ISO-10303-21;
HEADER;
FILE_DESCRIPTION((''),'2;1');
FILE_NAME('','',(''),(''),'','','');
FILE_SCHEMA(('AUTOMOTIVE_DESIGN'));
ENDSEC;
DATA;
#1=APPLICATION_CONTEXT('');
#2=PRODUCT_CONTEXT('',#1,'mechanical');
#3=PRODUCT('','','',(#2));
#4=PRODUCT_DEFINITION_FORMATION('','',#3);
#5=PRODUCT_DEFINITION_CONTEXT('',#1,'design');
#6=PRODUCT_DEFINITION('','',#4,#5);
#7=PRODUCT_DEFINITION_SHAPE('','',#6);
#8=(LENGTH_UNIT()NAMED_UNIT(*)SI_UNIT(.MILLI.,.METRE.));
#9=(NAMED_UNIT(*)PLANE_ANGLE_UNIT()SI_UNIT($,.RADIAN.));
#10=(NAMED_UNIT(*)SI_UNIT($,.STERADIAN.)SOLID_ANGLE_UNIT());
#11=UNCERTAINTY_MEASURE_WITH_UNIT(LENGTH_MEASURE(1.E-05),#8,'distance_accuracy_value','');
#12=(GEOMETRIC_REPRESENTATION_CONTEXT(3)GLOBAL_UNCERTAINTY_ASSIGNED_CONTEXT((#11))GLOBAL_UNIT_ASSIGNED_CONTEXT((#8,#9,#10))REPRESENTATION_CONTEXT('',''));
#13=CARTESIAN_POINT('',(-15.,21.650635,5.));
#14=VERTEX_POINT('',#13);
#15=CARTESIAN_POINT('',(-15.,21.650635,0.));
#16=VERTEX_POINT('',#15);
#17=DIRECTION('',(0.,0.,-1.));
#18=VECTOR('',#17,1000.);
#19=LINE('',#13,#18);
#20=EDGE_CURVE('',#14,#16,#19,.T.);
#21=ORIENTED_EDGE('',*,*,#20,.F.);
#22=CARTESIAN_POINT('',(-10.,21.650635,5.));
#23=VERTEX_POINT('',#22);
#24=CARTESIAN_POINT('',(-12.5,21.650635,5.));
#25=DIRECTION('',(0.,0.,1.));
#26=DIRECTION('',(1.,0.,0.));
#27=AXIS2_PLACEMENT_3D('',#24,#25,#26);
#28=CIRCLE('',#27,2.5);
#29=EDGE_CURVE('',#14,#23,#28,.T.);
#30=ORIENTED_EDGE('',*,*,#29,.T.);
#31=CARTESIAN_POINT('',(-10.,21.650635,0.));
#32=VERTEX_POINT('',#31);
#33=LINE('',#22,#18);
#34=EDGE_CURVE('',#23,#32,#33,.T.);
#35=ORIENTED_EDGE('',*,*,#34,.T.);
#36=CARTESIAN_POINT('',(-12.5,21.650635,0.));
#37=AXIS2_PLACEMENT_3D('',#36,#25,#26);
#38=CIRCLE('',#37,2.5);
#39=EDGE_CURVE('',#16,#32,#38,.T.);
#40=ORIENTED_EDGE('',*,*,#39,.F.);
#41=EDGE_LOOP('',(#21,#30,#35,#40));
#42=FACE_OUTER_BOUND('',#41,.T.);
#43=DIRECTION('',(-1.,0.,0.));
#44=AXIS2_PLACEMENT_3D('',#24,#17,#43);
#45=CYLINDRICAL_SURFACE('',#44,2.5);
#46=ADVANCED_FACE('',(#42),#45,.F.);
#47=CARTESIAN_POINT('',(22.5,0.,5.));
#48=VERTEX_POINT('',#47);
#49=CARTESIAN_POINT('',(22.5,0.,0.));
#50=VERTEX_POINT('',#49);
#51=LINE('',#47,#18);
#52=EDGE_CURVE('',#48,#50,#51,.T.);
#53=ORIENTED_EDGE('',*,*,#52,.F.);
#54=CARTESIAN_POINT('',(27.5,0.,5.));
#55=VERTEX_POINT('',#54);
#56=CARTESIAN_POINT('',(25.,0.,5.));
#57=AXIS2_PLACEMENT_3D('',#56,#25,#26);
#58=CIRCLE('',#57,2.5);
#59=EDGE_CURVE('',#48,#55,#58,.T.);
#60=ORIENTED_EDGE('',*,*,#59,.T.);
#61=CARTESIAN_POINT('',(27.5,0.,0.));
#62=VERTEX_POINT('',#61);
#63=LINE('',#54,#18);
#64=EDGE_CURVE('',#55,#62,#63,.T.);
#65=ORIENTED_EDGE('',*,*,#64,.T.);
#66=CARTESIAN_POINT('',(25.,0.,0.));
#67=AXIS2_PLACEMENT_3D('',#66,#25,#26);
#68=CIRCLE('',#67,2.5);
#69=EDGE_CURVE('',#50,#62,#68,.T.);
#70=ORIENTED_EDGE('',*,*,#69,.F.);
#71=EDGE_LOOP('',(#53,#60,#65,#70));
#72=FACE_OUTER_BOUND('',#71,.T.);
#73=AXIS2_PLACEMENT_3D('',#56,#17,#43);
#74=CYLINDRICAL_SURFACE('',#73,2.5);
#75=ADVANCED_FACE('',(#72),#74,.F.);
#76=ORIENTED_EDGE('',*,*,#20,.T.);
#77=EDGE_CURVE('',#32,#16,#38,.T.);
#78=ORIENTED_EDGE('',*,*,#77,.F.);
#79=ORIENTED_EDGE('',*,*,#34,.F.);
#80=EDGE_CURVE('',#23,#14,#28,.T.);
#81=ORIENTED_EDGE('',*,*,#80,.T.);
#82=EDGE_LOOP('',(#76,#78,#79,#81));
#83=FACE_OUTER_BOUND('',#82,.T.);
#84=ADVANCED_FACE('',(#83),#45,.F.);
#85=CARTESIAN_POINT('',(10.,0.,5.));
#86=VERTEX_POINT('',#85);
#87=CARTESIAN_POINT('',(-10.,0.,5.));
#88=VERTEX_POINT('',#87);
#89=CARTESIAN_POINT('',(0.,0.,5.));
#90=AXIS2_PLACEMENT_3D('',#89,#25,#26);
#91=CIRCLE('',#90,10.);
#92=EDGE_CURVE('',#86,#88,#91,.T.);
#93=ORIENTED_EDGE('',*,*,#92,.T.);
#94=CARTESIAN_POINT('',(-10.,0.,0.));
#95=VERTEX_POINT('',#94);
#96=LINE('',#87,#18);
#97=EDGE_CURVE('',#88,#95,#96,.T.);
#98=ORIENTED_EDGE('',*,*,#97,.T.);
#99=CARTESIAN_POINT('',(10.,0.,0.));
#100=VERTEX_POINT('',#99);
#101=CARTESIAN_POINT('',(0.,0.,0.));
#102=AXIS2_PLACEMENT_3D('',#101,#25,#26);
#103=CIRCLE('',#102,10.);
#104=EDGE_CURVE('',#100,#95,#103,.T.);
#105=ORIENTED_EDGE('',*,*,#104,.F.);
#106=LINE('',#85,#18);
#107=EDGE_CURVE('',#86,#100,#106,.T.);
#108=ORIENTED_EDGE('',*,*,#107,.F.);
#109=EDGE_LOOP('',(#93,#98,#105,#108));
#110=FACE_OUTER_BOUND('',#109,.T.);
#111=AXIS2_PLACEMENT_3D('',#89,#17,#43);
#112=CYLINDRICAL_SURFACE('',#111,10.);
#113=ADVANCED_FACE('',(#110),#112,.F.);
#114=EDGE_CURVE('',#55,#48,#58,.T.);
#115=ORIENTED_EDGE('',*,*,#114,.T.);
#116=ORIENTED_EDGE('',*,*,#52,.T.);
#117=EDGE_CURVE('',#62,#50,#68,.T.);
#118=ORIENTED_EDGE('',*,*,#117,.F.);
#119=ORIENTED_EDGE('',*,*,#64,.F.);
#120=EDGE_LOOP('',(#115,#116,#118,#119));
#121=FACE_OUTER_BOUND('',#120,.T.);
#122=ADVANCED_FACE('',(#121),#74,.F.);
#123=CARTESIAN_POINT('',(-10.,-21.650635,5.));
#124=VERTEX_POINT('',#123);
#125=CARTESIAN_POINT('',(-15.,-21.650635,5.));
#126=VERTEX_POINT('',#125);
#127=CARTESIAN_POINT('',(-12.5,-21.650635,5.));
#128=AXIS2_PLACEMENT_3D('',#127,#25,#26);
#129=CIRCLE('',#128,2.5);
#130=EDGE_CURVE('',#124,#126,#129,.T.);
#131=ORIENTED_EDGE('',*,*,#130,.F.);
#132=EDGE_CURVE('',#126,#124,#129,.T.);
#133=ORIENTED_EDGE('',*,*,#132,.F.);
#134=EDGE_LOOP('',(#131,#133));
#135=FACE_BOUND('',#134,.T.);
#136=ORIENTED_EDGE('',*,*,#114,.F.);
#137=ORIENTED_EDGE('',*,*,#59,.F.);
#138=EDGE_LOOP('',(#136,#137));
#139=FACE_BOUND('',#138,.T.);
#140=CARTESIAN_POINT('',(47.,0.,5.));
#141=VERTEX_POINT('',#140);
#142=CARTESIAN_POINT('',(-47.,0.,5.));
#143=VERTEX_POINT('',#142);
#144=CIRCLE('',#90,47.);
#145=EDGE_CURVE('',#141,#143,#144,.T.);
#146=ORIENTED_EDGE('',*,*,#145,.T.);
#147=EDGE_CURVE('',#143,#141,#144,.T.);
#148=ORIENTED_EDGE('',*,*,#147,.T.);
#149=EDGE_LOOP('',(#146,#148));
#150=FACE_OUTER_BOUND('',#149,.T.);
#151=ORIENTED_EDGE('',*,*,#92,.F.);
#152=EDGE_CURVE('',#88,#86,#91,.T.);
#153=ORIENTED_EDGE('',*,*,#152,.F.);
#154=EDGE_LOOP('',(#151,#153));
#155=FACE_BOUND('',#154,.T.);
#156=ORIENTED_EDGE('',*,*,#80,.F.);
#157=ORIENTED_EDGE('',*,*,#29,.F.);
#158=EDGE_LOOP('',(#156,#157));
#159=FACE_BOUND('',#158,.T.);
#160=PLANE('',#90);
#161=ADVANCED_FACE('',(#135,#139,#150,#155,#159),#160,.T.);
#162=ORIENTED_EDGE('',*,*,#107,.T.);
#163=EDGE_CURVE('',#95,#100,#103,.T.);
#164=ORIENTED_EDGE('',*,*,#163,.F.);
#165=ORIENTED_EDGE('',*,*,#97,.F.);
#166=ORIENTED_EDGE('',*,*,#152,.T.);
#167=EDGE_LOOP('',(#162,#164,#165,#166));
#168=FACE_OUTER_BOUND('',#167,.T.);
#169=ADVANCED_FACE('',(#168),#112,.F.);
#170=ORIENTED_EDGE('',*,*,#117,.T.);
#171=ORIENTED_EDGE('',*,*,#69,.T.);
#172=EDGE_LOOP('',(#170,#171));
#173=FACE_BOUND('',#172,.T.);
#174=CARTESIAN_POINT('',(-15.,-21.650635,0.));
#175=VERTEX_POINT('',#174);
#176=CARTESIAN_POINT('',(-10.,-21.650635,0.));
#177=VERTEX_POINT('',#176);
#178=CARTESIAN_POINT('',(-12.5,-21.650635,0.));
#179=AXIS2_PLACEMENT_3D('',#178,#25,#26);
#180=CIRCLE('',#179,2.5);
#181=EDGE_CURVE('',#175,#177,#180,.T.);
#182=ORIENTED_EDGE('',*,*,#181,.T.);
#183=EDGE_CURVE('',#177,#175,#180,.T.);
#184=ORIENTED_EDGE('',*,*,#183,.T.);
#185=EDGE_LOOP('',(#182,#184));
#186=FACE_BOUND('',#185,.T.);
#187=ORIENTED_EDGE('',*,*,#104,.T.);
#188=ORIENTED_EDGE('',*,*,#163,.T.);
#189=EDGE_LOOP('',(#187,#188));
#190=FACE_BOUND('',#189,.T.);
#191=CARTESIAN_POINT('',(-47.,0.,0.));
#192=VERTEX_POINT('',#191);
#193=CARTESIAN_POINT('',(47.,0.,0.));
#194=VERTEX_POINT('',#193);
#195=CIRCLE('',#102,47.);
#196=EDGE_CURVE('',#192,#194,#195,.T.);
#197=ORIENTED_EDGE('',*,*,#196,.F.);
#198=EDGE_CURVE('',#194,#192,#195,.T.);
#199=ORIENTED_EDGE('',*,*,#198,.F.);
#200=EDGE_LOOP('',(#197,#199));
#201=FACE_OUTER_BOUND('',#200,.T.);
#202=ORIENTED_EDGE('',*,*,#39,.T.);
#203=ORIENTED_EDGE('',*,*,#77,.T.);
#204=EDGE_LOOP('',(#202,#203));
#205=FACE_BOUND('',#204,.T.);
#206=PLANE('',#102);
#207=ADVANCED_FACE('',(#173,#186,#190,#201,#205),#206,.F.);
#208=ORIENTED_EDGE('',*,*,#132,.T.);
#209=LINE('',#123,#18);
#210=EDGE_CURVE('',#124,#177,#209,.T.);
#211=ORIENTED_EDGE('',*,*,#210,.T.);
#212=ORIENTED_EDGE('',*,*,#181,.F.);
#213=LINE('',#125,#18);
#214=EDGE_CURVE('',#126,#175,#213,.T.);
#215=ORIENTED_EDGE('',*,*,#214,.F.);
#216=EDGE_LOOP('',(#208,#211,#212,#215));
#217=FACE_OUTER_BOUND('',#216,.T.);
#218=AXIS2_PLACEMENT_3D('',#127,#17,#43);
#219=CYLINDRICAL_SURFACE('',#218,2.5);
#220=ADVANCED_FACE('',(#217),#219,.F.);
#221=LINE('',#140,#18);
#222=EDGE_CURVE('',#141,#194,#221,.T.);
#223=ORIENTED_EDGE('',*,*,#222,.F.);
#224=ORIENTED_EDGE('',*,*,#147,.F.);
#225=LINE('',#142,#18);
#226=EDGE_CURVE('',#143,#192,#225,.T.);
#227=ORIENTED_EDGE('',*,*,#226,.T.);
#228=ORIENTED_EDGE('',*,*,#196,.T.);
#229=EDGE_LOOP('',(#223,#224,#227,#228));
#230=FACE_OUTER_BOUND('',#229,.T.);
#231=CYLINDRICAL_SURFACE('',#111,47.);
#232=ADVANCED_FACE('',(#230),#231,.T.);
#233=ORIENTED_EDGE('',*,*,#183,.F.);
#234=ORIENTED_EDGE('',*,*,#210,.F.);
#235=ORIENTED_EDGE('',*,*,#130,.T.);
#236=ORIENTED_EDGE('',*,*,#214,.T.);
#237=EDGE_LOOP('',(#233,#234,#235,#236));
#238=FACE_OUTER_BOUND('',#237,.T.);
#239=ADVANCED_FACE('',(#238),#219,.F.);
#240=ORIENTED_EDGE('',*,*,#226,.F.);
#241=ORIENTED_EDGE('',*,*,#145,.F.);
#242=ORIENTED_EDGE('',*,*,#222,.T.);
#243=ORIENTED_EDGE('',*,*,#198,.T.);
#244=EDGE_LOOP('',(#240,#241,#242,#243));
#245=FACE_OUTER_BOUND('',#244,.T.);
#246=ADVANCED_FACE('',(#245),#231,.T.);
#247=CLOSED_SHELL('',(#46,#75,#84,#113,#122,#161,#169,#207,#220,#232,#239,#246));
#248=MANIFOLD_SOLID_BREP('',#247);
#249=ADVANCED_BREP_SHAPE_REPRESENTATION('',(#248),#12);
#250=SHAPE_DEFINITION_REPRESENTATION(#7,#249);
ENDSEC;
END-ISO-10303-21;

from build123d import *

# Parameters (mm, degrees)
SKETCH1_R           = 47
SKETCH1_R_2         = 10
SKETCH1_R_3         = 2.5
BOSS_EXTRUDE1_DEPTH = 5


with BuildPart() as part:
    # Sketch1 → Boss-Extrude1 (new body)
    with BuildSketch(Plane.XY):
        Circle(SKETCH1_R)
        Circle(SKETCH1_R_2, mode=Mode.SUBTRACT)
        with Locations((25, 0)):
            Circle(SKETCH1_R_3, mode=Mode.SUBTRACT)
        with Locations((-12.5, -21.650635095)):
            Circle(SKETCH1_R_3, mode=Mode.SUBTRACT)
        with Locations((-12.5, 21.650635095)):
            Circle(SKETCH1_R_3, mode=Mode.SUBTRACT)
    extrude(amount=BOSS_EXTRUDE1_DEPTH)


solid = part.part
